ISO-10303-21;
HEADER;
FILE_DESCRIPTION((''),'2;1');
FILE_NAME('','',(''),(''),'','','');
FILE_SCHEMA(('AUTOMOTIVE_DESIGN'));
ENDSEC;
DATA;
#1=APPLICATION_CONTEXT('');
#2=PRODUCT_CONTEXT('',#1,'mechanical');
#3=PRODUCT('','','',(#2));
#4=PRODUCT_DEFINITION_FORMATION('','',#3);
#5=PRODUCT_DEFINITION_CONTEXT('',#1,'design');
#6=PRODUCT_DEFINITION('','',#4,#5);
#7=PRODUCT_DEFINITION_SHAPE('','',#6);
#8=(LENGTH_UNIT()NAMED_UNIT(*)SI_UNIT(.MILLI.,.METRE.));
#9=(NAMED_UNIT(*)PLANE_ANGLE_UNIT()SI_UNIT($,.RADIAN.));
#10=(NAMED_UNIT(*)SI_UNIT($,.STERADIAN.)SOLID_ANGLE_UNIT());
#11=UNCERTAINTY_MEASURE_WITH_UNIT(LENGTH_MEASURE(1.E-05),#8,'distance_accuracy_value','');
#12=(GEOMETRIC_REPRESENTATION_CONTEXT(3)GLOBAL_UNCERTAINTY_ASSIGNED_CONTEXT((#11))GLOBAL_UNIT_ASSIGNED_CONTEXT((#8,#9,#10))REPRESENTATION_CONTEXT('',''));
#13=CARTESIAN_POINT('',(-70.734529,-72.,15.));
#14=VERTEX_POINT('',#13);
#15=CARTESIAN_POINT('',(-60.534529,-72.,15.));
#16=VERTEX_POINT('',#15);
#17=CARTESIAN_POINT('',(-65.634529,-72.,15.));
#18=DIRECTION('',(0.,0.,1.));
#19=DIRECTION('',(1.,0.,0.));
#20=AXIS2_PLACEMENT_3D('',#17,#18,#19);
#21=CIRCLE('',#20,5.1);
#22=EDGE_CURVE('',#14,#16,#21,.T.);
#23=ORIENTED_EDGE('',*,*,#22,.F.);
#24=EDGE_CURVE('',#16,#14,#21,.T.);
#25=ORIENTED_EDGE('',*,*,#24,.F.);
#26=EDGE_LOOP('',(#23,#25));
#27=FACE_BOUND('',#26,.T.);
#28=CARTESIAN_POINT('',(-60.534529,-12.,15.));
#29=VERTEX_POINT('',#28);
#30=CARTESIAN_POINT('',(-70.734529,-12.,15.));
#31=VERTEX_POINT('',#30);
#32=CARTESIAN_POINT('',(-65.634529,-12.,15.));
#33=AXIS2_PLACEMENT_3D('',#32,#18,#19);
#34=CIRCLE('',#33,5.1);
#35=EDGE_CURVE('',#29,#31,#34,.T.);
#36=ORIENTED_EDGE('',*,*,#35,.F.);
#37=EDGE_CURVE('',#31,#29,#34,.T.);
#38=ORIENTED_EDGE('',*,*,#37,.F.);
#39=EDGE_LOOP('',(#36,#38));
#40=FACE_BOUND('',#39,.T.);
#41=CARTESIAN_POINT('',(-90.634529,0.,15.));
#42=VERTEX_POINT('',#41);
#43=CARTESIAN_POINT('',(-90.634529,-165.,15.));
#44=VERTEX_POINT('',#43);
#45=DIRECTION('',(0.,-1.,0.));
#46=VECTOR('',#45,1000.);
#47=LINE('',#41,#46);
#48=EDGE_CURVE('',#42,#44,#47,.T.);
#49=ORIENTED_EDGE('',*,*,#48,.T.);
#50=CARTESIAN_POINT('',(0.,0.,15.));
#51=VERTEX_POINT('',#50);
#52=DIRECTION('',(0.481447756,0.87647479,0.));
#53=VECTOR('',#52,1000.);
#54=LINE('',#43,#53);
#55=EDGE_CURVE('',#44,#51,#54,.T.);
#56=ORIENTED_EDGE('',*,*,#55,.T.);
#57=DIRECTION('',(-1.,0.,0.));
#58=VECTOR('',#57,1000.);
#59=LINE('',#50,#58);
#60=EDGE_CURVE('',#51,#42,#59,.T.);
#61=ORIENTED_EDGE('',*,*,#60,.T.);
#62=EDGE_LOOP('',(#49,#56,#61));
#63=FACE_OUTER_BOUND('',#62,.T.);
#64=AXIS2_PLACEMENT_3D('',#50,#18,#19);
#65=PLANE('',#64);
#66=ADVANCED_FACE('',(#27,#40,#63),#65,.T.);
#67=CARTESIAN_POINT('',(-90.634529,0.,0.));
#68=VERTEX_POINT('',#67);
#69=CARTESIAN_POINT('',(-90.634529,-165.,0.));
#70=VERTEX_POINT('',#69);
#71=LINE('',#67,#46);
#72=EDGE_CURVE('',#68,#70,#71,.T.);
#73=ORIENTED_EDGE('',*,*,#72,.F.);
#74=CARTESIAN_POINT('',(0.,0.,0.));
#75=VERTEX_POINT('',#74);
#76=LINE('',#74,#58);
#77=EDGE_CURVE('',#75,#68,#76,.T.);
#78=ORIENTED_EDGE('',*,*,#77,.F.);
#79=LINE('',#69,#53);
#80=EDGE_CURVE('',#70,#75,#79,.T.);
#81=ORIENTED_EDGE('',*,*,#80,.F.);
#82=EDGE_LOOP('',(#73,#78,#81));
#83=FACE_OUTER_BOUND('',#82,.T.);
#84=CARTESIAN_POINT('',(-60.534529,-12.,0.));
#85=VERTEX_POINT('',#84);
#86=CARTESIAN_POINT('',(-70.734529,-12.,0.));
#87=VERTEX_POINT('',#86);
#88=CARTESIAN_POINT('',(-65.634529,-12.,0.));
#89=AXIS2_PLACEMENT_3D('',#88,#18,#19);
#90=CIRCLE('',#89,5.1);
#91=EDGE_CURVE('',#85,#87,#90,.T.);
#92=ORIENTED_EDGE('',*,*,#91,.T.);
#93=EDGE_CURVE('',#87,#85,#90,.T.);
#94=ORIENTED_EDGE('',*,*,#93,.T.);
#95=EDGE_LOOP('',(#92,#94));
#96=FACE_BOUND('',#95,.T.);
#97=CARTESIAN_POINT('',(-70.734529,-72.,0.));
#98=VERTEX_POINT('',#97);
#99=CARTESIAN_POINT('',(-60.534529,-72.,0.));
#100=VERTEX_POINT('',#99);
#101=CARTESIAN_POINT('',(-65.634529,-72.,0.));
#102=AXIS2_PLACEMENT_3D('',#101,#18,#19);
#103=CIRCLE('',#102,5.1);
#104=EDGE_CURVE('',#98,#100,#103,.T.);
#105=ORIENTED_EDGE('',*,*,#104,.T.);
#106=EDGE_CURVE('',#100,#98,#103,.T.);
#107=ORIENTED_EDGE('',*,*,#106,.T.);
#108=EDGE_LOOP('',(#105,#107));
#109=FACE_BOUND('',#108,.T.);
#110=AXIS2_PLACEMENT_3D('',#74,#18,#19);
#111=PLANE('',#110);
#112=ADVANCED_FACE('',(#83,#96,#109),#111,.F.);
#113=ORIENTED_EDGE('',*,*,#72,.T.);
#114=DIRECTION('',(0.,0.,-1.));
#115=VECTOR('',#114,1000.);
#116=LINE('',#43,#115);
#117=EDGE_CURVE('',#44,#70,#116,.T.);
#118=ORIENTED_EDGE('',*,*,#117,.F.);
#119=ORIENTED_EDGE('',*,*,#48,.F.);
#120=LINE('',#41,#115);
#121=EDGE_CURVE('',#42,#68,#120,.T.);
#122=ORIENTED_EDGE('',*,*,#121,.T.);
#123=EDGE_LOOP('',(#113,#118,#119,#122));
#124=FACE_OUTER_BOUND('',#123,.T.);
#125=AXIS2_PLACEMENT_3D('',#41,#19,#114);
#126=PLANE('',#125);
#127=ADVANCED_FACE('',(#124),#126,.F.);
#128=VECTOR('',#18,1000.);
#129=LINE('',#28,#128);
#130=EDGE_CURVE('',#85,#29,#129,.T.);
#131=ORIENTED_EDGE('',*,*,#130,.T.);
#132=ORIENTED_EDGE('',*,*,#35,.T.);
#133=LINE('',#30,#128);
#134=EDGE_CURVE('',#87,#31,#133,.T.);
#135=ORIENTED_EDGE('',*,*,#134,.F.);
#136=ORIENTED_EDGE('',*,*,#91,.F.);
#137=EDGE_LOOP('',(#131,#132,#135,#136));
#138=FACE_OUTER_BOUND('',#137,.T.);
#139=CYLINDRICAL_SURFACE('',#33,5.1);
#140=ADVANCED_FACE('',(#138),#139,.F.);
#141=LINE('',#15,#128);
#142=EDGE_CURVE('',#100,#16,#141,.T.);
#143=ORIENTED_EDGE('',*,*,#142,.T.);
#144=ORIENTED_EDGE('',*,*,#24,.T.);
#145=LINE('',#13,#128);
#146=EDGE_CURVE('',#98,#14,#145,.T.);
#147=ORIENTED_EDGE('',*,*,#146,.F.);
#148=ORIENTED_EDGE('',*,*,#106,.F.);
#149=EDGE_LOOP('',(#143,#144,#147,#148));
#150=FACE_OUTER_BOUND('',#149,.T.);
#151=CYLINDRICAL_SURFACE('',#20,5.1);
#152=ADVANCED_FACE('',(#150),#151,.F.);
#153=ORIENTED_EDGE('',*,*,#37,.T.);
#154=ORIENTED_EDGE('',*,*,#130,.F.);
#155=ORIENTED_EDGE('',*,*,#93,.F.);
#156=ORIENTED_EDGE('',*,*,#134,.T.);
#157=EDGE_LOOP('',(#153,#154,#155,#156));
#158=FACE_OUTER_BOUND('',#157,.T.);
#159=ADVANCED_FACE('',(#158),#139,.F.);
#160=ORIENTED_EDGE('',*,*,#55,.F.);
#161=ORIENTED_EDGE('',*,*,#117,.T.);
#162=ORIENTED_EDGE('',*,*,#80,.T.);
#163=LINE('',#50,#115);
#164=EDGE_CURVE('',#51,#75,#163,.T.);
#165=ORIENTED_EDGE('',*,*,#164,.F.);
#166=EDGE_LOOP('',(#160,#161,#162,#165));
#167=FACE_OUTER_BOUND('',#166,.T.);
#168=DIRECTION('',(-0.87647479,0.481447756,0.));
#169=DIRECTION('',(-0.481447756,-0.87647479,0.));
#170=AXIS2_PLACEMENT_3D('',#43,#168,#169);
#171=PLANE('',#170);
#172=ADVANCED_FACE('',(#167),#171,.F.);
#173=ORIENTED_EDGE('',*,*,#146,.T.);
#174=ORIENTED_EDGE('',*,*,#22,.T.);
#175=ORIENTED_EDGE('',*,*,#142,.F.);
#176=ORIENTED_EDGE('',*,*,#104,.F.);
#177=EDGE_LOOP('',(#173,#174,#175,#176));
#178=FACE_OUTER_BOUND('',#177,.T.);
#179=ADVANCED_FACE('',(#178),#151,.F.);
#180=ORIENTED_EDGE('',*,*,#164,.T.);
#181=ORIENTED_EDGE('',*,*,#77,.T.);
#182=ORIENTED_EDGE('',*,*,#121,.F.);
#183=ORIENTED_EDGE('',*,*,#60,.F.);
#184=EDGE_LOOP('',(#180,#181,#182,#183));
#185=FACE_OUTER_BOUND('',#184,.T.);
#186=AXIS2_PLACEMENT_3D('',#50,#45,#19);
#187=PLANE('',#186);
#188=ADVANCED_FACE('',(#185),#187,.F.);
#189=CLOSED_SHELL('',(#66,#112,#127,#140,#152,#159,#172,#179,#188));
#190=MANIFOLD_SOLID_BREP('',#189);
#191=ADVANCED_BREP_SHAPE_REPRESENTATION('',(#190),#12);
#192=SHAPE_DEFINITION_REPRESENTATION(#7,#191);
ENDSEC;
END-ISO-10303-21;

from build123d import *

# Parameters (mm, degrees)
SKETCH1_R              = 4.5
BOSS_EXTRUDE2_DEPTH    = 15
M12_TAPPED_HOLE1_D     = 10.2
M12_TAPPED_HOLE1_DEPTH = 29.25
M12_TAPPED_HOLE1_TIP   = 3.064389157


with BuildPart() as part:
    # Sketch1 → Boss-Extrude2 (new body)
    with BuildSketch(Plane.XY):
        Polygon((0, 0), (-90.634528925, 0), (-90.634528925, -165), align=None)
        with Locations((-65.634528925, -12)):
            Circle(SKETCH1_R, mode=Mode.SUBTRACT)
        with Locations((-65.634528925, -72)):
            Circle(SKETCH1_R, mode=Mode.SUBTRACT)
    extrude(amount=BOSS_EXTRUDE2_DEPTH)

    # M12 Tapped Hole1
    with Locations(Plane.XY.offset(15)):
        with Locations((-65.634528925, -12), (-65.634528925, -72)):
            Hole(M12_TAPPED_HOLE1_D / 2, depth=M12_TAPPED_HOLE1_DEPTH)
            with Locations((0, 0, -(M12_TAPPED_HOLE1_DEPTH + M12_TAPPED_HOLE1_TIP / 2))):  # 118° drill point
                Cone(0, M12_TAPPED_HOLE1_D / 2, M12_TAPPED_HOLE1_TIP, mode=Mode.SUBTRACT)


solid = part.part
